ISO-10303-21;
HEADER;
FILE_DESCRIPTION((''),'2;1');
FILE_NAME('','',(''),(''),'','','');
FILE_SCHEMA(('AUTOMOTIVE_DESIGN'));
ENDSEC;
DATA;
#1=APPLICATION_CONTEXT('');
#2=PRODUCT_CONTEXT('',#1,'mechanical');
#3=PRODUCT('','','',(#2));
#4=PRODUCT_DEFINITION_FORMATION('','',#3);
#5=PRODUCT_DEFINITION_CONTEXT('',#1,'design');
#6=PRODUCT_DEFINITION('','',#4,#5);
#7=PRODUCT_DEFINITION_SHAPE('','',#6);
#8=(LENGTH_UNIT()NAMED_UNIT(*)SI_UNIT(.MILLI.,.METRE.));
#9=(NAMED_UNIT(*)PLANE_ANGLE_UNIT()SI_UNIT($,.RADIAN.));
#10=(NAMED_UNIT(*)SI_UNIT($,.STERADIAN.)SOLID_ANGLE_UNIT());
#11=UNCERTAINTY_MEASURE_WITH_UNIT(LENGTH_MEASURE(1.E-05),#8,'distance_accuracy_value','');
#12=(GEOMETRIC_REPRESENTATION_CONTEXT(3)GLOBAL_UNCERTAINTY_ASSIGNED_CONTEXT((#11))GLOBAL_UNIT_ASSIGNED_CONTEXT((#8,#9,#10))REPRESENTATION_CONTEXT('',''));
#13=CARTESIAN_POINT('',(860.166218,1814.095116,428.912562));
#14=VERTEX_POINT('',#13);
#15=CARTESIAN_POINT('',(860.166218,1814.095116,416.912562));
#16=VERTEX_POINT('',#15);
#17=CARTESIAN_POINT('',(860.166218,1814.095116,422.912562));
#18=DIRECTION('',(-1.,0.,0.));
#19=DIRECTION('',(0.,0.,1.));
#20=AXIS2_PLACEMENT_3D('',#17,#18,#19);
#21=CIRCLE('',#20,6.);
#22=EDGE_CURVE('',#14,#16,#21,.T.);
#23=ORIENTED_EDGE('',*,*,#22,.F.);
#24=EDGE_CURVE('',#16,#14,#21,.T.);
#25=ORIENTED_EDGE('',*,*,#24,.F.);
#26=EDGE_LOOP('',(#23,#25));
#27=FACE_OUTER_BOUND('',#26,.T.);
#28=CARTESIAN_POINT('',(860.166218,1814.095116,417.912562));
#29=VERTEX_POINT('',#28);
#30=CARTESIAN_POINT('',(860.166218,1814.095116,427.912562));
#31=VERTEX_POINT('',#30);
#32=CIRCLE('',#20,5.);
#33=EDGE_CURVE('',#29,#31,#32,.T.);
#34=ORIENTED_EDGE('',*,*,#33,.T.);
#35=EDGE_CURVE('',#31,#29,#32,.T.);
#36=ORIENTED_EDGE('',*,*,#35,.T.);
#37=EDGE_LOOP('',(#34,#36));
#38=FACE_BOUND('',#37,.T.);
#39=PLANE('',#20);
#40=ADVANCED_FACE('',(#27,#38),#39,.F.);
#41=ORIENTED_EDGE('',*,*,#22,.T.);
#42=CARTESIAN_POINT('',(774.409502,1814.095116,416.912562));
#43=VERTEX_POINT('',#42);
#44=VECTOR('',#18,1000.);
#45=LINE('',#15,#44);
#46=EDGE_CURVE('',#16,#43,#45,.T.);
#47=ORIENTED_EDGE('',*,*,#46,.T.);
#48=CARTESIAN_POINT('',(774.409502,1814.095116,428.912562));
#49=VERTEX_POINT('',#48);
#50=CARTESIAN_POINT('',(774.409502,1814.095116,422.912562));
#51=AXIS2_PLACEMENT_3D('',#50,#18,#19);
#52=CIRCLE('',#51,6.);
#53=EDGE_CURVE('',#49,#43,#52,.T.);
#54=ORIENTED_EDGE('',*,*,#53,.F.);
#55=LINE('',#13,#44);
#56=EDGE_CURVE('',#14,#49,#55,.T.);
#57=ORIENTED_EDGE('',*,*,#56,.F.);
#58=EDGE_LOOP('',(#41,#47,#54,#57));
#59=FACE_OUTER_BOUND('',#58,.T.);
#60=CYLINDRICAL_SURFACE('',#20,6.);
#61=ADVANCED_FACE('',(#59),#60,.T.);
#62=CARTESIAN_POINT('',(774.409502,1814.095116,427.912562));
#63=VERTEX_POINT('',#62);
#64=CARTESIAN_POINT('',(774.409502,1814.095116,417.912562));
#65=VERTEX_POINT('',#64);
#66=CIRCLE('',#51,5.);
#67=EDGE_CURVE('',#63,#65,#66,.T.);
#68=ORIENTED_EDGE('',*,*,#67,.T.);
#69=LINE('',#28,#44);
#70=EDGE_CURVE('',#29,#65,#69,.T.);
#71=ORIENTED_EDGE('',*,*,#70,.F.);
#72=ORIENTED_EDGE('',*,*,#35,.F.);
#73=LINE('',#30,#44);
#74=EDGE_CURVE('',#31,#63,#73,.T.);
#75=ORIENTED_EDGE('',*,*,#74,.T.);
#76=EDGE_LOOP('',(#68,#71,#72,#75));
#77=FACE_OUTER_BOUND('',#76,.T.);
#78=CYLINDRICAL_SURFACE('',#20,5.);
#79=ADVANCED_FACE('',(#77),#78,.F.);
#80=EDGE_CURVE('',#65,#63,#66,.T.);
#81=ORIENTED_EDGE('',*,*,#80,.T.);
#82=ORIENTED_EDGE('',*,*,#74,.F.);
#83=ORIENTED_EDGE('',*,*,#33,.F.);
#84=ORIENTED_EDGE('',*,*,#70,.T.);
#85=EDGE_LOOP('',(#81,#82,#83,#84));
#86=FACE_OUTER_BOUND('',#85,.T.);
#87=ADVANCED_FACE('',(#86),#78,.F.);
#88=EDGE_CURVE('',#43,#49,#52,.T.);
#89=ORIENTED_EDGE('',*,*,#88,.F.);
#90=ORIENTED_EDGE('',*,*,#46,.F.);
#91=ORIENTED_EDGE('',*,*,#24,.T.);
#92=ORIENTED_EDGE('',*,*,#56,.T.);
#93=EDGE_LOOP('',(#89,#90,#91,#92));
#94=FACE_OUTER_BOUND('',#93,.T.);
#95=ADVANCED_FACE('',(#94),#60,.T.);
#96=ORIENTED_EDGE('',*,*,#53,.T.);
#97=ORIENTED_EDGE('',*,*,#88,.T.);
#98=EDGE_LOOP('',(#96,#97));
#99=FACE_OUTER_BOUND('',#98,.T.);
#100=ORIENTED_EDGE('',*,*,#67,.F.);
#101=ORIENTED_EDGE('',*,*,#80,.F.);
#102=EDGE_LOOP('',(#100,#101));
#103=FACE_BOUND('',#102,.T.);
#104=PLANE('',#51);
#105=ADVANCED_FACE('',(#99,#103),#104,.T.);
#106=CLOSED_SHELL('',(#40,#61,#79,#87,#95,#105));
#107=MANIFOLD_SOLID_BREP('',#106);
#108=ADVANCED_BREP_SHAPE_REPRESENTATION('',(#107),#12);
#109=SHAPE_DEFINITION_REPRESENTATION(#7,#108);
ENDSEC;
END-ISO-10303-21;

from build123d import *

# Parameters (mm, degrees)
SWEEP_1_PROFILE_R   = 6
SWEEP_1_PROFILE_R_2 = 5


with BuildPart() as part:
    # 扫描-薄件1: sweep along a curve in space
    with BuildLine() as sweep_1_path:
        Line((860.166218058, 1814.095116422, 422.912562332), (774.409502338, 1814.095116422, 422.912562332))
    # 扫描-薄件1 profile (on start of the path) → 扫描-薄件1 (sweep)
    with BuildSketch(Plane(origin=(860.166218058, 1814.095116422, 422.912562332), x_dir=(0, 0, -1), z_dir=(-1, 0, 0))):
        Circle(SWEEP_1_PROFILE_R)
        Circle(SWEEP_1_PROFILE_R_2, mode=Mode.SUBTRACT)
    sweep(path=sweep_1_path.line)


solid = part.part
